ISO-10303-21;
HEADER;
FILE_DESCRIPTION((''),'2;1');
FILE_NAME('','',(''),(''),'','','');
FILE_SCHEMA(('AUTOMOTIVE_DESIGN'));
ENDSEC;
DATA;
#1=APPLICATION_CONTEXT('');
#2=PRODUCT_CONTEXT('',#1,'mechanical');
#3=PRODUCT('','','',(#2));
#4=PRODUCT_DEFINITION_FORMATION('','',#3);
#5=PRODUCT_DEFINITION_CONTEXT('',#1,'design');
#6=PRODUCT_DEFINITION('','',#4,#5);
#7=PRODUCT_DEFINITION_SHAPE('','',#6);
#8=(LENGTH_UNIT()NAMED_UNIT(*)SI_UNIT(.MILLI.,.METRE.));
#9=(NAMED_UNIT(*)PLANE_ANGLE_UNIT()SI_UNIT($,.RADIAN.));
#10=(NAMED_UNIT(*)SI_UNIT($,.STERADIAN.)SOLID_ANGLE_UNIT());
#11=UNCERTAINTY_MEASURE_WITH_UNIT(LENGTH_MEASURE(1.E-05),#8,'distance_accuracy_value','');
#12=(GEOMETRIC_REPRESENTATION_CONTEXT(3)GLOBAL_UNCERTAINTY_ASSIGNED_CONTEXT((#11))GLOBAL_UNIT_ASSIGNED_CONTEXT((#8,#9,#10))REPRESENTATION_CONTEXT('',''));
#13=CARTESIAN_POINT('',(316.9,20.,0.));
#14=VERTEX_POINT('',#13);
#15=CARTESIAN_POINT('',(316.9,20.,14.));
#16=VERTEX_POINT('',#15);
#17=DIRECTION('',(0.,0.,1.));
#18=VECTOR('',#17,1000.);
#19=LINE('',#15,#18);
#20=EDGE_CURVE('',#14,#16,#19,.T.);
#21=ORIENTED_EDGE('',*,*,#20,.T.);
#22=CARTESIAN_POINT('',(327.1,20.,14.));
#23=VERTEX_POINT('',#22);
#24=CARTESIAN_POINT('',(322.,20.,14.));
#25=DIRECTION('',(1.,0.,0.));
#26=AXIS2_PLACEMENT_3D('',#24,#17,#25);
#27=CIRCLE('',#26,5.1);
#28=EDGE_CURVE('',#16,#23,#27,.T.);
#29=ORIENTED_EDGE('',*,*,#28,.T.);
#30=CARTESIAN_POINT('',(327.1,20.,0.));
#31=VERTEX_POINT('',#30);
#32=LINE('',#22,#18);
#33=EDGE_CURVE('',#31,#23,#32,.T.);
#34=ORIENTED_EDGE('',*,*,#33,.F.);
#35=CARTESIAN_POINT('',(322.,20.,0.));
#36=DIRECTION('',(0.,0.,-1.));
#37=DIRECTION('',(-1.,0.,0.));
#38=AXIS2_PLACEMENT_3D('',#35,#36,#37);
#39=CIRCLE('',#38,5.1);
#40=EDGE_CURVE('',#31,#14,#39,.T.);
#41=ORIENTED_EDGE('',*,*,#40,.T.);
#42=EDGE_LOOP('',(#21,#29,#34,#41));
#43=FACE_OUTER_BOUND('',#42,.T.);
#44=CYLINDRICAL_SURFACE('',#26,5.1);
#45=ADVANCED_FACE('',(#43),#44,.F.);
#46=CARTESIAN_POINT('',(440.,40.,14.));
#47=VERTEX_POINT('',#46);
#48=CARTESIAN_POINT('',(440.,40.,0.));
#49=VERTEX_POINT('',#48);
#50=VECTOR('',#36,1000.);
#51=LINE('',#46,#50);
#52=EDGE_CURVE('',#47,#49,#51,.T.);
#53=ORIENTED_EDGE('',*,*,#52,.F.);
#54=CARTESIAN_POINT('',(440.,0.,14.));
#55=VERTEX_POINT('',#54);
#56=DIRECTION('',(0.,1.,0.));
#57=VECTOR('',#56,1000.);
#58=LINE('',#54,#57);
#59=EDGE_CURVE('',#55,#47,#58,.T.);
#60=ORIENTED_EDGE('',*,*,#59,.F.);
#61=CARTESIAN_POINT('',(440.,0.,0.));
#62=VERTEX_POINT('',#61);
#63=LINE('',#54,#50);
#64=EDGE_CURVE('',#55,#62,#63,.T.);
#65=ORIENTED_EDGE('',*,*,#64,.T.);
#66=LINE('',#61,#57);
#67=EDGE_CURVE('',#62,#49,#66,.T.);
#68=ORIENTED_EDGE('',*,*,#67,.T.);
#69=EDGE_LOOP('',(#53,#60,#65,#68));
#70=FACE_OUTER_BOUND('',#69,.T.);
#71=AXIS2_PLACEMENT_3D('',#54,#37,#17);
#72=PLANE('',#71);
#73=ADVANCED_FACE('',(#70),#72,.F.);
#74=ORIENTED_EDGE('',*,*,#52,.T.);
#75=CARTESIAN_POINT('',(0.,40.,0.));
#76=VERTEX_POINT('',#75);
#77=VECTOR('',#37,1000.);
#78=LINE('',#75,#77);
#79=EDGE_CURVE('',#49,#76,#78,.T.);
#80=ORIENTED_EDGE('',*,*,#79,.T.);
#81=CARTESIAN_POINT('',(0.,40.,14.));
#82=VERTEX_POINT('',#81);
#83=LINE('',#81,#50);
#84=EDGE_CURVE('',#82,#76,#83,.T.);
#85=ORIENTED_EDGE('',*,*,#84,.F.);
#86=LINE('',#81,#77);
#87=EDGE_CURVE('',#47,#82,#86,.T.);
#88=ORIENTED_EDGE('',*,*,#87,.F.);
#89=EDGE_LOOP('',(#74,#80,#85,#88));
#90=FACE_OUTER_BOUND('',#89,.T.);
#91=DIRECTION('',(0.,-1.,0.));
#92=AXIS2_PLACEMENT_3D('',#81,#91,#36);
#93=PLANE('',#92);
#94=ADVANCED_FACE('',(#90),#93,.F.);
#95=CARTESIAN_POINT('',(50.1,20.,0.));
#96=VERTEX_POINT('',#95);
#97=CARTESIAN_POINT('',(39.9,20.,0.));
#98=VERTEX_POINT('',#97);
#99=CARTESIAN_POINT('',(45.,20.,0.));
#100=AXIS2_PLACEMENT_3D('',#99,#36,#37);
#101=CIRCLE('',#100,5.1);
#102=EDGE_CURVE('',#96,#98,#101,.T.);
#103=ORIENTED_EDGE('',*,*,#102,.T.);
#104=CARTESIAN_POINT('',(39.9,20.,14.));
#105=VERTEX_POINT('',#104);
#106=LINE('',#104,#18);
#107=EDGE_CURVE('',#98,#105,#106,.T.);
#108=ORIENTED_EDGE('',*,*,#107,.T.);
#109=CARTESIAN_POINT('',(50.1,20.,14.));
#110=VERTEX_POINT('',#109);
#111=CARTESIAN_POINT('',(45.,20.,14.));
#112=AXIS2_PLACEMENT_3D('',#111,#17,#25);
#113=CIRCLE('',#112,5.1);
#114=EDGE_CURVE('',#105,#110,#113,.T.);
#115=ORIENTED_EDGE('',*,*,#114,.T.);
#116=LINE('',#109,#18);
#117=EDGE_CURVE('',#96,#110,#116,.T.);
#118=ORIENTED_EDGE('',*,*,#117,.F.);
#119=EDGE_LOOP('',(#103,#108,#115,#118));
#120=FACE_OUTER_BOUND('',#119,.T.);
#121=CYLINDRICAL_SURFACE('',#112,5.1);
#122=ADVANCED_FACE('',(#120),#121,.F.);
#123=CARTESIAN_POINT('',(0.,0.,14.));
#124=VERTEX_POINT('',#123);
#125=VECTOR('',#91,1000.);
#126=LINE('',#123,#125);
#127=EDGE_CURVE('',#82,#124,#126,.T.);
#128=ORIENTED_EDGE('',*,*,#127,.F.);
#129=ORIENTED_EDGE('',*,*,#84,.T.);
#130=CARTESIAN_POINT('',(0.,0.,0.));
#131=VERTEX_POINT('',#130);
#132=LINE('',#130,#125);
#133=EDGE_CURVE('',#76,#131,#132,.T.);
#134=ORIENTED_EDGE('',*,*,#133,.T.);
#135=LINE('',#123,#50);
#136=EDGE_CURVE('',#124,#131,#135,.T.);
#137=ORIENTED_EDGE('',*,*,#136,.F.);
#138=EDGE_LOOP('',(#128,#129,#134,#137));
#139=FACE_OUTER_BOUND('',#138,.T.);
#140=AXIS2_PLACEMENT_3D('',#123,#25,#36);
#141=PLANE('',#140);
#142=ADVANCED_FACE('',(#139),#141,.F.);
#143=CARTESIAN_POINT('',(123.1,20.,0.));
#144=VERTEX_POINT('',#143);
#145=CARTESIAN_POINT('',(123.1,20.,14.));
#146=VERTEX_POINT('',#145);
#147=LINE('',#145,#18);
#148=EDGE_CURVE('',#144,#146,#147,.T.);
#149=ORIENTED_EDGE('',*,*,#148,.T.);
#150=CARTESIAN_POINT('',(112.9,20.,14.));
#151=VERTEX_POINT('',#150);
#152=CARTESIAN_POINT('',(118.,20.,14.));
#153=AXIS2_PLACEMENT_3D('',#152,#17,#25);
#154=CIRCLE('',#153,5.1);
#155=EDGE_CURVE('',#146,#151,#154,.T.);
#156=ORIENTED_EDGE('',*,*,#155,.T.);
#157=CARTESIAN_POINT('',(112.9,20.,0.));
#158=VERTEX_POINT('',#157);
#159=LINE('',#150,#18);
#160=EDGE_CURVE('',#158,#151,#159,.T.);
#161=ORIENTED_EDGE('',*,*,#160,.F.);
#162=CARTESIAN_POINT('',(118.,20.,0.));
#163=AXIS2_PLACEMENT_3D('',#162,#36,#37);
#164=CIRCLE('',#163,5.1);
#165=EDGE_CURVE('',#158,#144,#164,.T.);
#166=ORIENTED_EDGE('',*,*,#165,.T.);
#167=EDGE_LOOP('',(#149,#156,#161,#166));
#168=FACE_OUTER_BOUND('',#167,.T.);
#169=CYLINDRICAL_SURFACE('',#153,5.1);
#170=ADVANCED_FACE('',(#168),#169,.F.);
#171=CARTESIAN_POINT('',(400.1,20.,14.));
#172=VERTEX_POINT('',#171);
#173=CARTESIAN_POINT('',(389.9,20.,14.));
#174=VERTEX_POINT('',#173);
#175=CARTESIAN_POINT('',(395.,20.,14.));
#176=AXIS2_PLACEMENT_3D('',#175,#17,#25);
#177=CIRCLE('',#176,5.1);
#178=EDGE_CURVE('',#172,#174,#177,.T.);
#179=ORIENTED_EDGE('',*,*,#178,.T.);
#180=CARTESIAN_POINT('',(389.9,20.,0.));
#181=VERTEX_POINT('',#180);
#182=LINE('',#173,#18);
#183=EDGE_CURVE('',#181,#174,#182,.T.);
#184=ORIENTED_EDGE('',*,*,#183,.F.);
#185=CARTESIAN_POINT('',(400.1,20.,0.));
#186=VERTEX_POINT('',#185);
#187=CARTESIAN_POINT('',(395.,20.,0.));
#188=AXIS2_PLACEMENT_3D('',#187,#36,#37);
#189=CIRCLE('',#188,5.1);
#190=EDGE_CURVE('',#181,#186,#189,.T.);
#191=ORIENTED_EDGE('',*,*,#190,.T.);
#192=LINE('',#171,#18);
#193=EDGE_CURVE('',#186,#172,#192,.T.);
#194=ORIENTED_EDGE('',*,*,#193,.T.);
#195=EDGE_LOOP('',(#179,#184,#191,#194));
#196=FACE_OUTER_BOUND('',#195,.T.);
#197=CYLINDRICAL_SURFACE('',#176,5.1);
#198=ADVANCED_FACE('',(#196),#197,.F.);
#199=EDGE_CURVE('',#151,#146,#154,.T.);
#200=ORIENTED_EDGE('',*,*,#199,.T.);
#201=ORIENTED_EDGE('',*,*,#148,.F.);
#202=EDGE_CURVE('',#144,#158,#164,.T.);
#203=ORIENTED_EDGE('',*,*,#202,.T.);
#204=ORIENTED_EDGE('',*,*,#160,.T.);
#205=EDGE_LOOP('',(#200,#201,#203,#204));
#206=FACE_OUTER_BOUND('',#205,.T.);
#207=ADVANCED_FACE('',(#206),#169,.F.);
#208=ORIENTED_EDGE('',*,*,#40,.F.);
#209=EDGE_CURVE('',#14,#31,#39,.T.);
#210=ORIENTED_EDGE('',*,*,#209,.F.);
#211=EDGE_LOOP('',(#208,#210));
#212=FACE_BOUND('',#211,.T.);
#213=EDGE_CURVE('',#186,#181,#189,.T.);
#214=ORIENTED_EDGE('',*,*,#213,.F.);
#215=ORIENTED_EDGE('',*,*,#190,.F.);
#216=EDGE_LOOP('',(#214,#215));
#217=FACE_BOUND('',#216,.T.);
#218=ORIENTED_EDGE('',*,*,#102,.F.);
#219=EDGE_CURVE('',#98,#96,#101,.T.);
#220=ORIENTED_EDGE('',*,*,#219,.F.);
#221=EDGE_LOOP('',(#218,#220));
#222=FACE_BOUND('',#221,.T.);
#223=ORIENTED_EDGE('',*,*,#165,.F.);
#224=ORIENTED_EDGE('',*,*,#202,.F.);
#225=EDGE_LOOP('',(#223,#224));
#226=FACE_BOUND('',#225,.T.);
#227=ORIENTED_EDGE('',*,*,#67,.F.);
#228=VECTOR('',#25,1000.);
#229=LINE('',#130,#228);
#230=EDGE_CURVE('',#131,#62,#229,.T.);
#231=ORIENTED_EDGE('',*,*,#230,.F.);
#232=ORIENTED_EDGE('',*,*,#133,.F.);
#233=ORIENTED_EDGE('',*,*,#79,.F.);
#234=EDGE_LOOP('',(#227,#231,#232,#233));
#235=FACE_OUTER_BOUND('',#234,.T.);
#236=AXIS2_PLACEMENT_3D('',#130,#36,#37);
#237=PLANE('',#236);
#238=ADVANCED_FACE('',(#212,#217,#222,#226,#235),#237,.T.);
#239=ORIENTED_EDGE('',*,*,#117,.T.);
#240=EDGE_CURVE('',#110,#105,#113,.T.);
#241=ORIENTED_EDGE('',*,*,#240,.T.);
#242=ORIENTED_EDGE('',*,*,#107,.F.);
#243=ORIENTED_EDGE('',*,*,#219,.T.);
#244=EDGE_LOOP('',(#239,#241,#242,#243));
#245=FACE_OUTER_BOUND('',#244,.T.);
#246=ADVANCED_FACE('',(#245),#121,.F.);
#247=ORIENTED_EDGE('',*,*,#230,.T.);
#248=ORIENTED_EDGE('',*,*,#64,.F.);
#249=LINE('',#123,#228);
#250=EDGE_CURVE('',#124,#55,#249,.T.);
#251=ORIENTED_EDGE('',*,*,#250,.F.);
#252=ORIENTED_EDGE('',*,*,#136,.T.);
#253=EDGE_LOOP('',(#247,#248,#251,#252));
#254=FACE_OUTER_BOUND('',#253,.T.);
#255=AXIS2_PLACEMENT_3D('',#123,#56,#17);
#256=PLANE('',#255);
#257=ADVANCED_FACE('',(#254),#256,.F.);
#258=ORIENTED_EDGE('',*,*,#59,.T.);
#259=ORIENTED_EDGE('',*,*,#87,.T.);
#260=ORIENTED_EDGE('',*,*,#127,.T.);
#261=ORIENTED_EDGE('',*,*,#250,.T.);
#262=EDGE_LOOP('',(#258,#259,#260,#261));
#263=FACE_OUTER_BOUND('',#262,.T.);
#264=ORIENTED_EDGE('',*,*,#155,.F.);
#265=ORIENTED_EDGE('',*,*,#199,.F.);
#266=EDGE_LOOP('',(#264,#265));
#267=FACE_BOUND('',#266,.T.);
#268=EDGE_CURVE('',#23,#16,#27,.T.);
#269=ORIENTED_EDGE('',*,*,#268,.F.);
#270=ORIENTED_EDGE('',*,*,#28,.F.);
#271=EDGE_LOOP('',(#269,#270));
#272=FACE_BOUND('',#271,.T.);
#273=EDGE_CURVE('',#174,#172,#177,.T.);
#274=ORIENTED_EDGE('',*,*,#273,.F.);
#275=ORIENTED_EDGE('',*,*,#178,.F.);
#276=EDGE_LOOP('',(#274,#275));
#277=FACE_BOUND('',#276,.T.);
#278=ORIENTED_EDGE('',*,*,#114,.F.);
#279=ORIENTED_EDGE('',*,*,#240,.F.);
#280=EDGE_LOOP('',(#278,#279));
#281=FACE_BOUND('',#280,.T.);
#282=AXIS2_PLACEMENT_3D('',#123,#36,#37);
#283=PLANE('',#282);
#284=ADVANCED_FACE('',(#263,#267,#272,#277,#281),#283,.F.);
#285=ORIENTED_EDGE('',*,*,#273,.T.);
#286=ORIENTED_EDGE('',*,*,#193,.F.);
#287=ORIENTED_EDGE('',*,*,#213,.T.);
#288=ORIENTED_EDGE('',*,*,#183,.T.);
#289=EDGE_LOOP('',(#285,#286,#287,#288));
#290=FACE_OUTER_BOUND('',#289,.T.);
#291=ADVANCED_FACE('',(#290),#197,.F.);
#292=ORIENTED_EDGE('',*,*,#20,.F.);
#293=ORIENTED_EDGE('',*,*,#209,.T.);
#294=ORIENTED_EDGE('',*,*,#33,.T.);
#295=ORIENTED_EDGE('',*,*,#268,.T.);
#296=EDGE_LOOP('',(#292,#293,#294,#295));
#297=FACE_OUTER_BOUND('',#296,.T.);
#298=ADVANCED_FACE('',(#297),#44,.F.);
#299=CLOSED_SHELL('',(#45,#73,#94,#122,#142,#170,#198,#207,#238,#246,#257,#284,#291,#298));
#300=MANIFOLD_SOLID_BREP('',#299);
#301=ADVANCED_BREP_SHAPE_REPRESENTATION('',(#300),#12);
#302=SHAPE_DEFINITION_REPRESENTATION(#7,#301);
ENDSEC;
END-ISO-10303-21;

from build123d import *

# Parameters (mm, degrees)
SKETCH_1_W              = 440
SKETCH_1_H              = 40
EXTRUDE_1_DEPTH         = 14
HOLE_WIZARD_M12_1_D     = 10.2
HOLE_WIZARD_M12_1_DEPTH = 29.25
HOLE_WIZARD_M12_1_TIP   = 3.064389157


with BuildPart() as part:
    # 草图1 → 凸台-拉伸1 (new body)
    with BuildSketch(Plane.XY):
        with Locations((220, 20)):
            Rectangle(SKETCH_1_W, SKETCH_1_H)
    extrude(amount=EXTRUDE_1_DEPTH)

    # M12 螺纹孔1
    with Locations(Plane(origin=(45, 20, 14), x_dir=(1, 0, 0), z_dir=(0, 0, 1))):
        with Locations((0, 0), (73, 0), (350, 0), (277, 0)):
            Hole(HOLE_WIZARD_M12_1_D / 2, depth=HOLE_WIZARD_M12_1_DEPTH)
            with Locations((0, 0, -(HOLE_WIZARD_M12_1_DEPTH + HOLE_WIZARD_M12_1_TIP / 2))):  # 118° drill point
                Cone(0, HOLE_WIZARD_M12_1_D / 2, HOLE_WIZARD_M12_1_TIP, mode=Mode.SUBTRACT)


solid = part.part
